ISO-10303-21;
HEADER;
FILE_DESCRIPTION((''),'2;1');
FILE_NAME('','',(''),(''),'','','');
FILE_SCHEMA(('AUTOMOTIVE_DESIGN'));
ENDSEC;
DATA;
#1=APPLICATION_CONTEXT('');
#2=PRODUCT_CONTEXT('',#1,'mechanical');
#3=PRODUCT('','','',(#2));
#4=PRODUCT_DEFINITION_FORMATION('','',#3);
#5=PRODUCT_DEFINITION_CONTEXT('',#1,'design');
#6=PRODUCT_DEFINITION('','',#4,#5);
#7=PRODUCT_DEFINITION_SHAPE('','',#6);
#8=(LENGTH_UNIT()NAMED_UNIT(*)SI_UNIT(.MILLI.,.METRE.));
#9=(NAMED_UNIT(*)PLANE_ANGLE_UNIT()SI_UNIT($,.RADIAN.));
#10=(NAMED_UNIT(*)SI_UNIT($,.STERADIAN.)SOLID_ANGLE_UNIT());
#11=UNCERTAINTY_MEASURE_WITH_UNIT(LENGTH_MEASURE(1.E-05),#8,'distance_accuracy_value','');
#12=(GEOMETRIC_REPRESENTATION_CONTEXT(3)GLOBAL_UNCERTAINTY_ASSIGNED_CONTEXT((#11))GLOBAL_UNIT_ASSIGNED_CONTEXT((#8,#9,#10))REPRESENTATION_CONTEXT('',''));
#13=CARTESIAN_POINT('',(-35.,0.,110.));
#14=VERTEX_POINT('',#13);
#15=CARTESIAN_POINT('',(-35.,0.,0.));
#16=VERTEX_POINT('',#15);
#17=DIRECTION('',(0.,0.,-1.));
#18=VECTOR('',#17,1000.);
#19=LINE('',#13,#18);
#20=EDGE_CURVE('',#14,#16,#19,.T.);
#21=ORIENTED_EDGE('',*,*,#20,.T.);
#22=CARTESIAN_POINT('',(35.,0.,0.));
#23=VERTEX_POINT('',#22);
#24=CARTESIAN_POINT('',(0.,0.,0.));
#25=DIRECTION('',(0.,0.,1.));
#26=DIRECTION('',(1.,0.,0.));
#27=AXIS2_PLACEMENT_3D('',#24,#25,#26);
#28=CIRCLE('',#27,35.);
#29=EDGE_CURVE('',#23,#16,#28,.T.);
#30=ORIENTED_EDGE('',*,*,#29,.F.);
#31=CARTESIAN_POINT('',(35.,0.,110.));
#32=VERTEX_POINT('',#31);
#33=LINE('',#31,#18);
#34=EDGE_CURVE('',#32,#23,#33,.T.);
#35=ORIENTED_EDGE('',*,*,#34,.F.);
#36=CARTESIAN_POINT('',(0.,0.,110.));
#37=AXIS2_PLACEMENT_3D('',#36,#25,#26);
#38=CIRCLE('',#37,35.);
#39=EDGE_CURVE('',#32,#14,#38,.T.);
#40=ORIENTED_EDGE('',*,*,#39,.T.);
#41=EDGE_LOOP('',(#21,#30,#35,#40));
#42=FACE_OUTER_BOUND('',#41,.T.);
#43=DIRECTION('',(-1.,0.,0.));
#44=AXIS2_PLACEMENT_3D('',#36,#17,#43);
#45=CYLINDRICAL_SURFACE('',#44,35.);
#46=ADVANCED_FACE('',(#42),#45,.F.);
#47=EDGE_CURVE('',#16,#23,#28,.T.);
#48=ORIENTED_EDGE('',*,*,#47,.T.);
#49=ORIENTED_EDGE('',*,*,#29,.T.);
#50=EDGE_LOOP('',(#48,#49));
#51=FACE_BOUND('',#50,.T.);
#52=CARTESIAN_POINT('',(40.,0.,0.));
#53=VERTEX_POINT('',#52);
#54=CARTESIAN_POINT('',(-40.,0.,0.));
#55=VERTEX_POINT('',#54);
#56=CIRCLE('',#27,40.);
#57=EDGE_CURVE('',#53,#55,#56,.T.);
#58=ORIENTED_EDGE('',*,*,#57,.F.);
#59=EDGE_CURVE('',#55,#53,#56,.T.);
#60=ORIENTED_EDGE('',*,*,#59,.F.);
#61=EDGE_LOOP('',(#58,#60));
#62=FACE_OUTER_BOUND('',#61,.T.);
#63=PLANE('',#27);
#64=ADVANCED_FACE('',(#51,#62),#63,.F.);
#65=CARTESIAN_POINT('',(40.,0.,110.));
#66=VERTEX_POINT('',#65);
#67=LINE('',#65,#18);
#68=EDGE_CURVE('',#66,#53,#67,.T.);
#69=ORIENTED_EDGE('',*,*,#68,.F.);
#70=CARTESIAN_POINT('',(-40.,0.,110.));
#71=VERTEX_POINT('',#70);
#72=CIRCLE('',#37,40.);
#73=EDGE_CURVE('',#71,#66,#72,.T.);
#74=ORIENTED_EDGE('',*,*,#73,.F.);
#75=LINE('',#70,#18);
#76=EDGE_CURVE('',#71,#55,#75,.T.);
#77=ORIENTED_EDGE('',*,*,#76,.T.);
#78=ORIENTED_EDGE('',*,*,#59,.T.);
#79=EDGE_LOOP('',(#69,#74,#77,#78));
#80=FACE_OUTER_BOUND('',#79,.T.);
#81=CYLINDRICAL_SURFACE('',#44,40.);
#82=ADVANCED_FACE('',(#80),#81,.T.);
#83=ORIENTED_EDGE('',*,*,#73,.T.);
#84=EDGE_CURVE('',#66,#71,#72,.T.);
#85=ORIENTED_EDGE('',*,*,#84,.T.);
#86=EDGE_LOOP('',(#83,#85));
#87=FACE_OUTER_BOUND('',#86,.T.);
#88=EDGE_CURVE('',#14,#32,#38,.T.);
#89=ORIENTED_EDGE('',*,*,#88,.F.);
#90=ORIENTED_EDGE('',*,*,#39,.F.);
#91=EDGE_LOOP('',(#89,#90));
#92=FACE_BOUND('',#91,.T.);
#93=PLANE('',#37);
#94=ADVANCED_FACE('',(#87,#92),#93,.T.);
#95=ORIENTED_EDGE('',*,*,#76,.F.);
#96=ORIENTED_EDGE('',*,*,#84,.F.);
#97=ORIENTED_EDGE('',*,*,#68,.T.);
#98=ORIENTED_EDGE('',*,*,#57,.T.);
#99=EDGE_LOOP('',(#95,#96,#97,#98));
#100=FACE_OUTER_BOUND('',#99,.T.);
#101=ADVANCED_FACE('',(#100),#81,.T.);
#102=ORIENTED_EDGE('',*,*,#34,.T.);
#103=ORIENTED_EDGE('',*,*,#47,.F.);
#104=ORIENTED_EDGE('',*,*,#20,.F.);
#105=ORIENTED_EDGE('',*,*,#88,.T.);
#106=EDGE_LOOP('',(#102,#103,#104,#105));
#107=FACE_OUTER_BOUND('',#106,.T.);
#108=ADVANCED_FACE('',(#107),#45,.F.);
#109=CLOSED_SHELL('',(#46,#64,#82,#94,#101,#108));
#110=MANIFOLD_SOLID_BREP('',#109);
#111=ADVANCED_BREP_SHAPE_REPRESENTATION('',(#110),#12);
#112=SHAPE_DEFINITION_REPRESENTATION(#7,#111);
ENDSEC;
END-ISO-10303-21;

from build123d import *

# Parameters (mm, degrees)
SLEEVE_PROFILE_80X_70_R   = 40
SLEEVE_PROFILE_80X_70_R_2 = 35
SLEEVE_BODY_L110_DEPTH    = 110


with BuildPart() as part:
    # Sleeve Profile Ø80xØ70 → Sleeve Body L110 (new body)
    with BuildSketch(Plane.XY):
        Circle(SLEEVE_PROFILE_80X_70_R)
        Circle(SLEEVE_PROFILE_80X_70_R_2, mode=Mode.SUBTRACT)
    extrude(amount=SLEEVE_BODY_L110_DEPTH)


solid = part.part
